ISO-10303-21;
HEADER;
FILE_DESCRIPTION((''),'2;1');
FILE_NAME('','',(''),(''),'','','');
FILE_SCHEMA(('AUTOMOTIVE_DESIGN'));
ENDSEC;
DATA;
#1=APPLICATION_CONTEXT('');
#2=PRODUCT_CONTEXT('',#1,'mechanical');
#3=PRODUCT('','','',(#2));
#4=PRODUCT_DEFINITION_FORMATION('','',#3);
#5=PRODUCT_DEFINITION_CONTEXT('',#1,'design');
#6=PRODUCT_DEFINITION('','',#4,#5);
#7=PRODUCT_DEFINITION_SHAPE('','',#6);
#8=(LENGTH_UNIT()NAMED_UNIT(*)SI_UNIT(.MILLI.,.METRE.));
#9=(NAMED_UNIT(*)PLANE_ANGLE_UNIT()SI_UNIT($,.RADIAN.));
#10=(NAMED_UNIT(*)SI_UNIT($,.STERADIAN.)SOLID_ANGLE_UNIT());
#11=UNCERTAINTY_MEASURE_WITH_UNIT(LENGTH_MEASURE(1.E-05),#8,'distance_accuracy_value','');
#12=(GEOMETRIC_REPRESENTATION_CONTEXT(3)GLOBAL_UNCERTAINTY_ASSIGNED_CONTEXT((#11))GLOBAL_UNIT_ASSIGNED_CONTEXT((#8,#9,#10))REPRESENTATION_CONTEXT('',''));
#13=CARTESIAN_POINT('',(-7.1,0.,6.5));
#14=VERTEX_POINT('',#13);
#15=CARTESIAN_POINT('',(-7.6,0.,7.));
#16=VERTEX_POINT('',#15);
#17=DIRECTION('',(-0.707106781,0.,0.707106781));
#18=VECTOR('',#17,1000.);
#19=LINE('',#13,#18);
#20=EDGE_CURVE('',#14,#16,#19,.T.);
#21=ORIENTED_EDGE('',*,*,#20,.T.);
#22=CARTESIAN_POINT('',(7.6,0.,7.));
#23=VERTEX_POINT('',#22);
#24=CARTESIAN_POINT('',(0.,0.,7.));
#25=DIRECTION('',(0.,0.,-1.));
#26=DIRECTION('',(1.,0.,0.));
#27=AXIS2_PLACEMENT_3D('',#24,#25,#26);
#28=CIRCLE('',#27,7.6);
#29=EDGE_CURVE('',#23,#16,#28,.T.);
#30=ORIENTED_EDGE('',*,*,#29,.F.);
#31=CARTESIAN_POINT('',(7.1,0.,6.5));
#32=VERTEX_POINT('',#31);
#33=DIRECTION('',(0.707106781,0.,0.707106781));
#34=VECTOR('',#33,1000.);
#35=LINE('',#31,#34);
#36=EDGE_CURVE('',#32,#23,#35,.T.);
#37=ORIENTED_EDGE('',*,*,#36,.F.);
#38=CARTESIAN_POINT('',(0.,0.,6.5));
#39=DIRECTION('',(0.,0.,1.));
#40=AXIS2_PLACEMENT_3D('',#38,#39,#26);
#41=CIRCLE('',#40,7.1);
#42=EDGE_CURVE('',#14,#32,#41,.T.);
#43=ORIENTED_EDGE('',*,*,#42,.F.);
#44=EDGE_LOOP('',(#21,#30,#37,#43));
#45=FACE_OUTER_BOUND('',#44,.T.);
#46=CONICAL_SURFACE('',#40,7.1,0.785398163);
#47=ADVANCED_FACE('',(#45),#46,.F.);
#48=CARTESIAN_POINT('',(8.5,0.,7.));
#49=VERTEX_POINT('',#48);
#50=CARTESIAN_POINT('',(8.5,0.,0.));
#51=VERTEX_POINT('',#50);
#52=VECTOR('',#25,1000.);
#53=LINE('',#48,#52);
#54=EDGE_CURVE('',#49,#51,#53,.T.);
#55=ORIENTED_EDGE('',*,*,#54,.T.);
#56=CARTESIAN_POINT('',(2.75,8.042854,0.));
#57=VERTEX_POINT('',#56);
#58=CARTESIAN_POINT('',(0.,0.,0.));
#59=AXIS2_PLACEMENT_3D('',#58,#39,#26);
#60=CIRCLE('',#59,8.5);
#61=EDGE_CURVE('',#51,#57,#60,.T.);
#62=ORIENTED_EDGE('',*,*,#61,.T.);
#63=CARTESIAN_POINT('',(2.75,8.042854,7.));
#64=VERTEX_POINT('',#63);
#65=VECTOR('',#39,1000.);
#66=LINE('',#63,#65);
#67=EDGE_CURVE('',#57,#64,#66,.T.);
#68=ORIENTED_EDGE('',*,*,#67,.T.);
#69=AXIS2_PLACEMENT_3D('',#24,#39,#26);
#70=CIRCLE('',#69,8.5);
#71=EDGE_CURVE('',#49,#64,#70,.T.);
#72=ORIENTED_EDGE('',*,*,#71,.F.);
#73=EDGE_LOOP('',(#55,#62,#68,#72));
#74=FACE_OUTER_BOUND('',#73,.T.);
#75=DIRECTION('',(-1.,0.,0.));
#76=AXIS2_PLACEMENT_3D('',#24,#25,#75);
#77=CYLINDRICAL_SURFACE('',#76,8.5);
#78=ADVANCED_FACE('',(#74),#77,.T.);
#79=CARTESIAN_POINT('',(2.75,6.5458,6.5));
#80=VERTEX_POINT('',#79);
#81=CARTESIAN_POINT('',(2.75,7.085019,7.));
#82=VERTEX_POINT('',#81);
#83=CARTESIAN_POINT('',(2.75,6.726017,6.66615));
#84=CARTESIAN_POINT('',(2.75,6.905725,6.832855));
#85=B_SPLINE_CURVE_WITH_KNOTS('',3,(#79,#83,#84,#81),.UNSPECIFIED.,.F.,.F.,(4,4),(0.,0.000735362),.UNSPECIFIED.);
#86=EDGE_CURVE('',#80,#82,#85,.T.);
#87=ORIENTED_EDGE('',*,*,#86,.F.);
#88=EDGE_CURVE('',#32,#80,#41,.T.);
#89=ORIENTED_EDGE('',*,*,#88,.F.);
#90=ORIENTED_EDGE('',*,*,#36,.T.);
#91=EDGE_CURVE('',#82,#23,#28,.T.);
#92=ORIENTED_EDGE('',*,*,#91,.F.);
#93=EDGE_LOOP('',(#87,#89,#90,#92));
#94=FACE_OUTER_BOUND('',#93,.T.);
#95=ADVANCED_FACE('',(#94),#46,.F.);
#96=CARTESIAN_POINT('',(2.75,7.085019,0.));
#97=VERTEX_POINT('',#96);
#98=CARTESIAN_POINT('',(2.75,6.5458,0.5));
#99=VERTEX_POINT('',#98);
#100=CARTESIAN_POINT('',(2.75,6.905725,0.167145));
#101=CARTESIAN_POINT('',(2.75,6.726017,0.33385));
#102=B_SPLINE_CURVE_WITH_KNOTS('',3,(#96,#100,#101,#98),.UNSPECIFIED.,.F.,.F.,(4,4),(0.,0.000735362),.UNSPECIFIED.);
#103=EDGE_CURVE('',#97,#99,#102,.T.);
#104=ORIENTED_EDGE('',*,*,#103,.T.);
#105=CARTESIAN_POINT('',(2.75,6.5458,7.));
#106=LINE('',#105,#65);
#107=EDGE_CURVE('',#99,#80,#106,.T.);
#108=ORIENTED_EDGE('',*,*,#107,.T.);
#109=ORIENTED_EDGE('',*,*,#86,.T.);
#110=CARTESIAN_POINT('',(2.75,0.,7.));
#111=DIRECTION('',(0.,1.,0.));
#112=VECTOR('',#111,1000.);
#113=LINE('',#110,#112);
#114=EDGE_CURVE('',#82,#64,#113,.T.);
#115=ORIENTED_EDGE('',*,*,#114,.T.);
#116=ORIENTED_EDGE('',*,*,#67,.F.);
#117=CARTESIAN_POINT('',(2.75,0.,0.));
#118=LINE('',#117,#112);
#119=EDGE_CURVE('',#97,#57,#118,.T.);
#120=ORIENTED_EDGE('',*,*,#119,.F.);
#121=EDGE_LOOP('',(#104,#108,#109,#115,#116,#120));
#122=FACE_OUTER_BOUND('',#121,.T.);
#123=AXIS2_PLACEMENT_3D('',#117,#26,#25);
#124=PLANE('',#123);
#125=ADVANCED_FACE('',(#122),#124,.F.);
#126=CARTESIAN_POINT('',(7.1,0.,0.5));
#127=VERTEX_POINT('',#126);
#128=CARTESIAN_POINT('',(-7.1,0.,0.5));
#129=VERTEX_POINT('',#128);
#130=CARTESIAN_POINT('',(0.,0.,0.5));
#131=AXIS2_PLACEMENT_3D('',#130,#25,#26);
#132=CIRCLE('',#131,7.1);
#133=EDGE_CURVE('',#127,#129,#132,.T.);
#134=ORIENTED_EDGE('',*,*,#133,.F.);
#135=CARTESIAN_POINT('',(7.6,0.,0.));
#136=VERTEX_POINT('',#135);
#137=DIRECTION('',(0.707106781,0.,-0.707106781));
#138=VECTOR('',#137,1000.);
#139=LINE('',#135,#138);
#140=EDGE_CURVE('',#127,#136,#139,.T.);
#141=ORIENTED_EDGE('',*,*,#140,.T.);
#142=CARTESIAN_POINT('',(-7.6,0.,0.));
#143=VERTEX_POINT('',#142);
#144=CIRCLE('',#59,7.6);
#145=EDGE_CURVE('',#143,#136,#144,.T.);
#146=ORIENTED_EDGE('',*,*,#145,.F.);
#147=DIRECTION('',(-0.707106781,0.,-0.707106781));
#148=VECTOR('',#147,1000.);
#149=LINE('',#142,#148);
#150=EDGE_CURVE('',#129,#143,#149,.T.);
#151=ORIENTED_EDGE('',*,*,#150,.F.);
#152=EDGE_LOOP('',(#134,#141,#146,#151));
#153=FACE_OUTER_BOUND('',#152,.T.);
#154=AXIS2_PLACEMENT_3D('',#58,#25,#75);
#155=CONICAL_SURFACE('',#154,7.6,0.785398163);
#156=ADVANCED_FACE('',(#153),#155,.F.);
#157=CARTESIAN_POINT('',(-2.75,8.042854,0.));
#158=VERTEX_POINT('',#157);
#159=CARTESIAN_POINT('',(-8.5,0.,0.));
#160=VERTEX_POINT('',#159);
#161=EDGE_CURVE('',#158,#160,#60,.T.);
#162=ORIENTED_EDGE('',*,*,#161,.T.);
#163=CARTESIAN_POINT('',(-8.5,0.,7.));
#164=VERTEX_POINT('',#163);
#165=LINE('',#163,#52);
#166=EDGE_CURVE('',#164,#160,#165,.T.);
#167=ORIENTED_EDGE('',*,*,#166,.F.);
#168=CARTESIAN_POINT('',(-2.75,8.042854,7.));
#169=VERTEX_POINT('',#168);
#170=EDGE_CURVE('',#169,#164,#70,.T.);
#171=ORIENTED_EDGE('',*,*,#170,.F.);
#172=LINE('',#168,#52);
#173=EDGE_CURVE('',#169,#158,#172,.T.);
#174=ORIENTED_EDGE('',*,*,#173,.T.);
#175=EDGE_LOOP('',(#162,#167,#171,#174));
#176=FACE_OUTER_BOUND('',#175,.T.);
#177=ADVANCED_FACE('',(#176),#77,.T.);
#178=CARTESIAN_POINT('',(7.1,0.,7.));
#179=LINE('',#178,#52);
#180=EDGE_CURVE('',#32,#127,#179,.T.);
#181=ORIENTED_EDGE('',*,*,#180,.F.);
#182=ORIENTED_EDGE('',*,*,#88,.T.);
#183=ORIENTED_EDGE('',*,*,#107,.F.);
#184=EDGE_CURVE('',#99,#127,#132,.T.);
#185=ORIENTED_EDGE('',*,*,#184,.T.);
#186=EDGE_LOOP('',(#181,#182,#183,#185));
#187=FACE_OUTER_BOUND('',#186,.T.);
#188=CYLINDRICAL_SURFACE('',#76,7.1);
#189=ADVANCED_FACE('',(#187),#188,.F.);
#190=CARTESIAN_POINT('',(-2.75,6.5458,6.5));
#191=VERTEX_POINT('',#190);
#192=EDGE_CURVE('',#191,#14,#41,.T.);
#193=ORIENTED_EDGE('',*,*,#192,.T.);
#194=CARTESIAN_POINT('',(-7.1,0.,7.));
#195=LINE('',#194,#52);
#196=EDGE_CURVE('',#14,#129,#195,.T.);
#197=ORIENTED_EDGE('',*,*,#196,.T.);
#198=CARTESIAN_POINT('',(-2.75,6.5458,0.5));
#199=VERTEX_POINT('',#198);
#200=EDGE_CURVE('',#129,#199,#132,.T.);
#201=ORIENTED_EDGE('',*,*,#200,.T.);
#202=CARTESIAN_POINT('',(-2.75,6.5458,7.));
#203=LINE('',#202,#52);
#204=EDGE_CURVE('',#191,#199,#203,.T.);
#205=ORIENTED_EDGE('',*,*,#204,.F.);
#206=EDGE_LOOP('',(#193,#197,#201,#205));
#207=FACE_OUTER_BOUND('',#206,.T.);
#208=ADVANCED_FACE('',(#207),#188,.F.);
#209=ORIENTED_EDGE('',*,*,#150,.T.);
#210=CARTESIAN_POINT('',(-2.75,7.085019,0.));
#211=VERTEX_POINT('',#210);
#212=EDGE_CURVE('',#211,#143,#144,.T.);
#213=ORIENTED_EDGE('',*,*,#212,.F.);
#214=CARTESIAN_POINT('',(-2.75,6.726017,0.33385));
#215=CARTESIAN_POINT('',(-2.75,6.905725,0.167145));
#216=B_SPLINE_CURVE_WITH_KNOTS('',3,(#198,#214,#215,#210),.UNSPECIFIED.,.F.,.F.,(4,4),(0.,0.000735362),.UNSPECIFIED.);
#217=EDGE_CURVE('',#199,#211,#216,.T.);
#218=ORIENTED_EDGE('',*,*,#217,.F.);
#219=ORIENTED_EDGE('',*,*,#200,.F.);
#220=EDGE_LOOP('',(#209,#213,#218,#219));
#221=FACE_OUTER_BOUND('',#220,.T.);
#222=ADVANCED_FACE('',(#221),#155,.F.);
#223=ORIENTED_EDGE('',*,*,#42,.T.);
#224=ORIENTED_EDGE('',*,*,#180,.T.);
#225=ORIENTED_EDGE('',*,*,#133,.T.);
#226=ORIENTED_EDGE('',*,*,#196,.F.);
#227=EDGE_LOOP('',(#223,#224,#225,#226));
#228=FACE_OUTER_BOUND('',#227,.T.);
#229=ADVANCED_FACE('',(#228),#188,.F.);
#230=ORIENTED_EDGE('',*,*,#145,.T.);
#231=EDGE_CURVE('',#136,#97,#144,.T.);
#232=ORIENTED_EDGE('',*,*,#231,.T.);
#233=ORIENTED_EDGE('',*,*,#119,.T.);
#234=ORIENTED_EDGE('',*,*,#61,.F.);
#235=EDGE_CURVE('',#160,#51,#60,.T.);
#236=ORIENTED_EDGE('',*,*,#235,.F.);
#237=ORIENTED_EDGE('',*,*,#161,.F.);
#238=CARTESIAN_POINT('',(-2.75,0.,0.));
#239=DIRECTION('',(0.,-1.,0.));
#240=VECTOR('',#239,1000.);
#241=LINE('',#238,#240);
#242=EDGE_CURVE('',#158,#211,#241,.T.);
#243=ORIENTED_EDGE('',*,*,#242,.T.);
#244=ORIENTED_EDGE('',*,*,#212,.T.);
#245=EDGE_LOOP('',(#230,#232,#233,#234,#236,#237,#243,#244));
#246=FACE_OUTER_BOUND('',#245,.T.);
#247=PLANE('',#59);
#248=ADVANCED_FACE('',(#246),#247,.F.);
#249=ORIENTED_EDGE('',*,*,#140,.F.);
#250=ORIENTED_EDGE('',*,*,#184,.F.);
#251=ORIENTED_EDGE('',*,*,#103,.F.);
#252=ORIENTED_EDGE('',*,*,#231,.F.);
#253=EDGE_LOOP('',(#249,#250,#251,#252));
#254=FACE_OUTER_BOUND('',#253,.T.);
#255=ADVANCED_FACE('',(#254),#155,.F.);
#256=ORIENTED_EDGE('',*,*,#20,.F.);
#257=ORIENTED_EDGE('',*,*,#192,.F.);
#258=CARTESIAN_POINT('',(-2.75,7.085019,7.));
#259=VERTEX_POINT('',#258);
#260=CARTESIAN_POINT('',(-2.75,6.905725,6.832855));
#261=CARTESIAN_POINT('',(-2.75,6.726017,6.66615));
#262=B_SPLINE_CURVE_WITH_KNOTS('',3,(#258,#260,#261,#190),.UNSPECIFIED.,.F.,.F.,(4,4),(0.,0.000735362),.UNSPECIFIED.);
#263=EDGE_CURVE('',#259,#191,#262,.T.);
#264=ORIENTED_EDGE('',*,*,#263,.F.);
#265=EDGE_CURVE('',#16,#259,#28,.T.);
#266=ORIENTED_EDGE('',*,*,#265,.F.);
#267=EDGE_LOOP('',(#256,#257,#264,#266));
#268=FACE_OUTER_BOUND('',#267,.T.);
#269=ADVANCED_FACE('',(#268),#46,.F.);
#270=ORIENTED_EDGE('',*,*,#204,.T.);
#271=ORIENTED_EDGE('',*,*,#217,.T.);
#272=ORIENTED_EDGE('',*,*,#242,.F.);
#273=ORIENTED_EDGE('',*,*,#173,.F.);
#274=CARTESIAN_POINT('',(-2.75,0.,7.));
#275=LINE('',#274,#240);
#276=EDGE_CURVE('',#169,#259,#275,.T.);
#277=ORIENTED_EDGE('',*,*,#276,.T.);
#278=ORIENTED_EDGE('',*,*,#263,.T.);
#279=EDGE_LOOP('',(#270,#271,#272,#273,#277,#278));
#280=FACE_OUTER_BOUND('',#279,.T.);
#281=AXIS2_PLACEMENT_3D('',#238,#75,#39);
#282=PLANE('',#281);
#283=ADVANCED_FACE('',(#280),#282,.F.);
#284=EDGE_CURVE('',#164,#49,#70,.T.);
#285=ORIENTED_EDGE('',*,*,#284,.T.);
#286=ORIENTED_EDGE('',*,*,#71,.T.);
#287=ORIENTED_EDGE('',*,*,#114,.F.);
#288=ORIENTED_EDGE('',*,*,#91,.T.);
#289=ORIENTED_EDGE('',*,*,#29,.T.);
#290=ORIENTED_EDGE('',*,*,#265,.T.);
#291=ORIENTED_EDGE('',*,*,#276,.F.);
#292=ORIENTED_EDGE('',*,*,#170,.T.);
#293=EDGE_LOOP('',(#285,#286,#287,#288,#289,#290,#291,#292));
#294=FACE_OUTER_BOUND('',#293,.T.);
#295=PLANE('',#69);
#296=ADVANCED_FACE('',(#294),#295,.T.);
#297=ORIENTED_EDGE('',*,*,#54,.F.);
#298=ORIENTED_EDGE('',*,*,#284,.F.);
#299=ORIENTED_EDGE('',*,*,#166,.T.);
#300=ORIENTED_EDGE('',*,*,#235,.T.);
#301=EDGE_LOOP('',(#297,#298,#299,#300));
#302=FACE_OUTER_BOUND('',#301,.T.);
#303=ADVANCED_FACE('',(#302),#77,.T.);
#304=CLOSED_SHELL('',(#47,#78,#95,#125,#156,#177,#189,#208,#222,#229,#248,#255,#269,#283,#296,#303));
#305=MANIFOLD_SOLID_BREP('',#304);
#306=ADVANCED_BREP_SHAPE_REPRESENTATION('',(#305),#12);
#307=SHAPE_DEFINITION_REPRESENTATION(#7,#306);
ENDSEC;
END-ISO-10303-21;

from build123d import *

# Parameters (mm, degrees)
SKETCH1_R           = 8.5
SKETCH1_R_2         = 7.1
BOSS_EXTRUDE1_DEPTH = 7
SKETCH2_W           = 5.5
SKETCH2_H           = 15
CUT_EXTRUDE1_DEPTH  = 14.910427743
CHAMFER1_SIZE       = 0.5


with BuildPart() as part:
    # Sketch1 → Boss-Extrude1 (new body)
    with BuildSketch(Plane.XY):
        Circle(SKETCH1_R)
        Circle(SKETCH1_R_2, mode=Mode.SUBTRACT)
    extrude(amount=BOSS_EXTRUDE1_DEPTH)

    # Sketch2 → Cut-Extrude1 (cut, through all)
    with BuildSketch(Plane.XY.offset(7)):
        with Locations((0, 7.5)):
            Rectangle(SKETCH2_W, SKETCH2_H)
    extrude(amount=-CUT_EXTRUDE1_DEPTH, mode=Mode.SUBTRACT)

    # Chamfer1
    chamfer1_edges = [part.edges().sort_by_distance(p)[0] for p in [
        (0, -7.1, 0),
        (0, -7.1, 7),
    ]]
    chamfer(chamfer1_edges, length=CHAMFER1_SIZE)


solid = part.part
